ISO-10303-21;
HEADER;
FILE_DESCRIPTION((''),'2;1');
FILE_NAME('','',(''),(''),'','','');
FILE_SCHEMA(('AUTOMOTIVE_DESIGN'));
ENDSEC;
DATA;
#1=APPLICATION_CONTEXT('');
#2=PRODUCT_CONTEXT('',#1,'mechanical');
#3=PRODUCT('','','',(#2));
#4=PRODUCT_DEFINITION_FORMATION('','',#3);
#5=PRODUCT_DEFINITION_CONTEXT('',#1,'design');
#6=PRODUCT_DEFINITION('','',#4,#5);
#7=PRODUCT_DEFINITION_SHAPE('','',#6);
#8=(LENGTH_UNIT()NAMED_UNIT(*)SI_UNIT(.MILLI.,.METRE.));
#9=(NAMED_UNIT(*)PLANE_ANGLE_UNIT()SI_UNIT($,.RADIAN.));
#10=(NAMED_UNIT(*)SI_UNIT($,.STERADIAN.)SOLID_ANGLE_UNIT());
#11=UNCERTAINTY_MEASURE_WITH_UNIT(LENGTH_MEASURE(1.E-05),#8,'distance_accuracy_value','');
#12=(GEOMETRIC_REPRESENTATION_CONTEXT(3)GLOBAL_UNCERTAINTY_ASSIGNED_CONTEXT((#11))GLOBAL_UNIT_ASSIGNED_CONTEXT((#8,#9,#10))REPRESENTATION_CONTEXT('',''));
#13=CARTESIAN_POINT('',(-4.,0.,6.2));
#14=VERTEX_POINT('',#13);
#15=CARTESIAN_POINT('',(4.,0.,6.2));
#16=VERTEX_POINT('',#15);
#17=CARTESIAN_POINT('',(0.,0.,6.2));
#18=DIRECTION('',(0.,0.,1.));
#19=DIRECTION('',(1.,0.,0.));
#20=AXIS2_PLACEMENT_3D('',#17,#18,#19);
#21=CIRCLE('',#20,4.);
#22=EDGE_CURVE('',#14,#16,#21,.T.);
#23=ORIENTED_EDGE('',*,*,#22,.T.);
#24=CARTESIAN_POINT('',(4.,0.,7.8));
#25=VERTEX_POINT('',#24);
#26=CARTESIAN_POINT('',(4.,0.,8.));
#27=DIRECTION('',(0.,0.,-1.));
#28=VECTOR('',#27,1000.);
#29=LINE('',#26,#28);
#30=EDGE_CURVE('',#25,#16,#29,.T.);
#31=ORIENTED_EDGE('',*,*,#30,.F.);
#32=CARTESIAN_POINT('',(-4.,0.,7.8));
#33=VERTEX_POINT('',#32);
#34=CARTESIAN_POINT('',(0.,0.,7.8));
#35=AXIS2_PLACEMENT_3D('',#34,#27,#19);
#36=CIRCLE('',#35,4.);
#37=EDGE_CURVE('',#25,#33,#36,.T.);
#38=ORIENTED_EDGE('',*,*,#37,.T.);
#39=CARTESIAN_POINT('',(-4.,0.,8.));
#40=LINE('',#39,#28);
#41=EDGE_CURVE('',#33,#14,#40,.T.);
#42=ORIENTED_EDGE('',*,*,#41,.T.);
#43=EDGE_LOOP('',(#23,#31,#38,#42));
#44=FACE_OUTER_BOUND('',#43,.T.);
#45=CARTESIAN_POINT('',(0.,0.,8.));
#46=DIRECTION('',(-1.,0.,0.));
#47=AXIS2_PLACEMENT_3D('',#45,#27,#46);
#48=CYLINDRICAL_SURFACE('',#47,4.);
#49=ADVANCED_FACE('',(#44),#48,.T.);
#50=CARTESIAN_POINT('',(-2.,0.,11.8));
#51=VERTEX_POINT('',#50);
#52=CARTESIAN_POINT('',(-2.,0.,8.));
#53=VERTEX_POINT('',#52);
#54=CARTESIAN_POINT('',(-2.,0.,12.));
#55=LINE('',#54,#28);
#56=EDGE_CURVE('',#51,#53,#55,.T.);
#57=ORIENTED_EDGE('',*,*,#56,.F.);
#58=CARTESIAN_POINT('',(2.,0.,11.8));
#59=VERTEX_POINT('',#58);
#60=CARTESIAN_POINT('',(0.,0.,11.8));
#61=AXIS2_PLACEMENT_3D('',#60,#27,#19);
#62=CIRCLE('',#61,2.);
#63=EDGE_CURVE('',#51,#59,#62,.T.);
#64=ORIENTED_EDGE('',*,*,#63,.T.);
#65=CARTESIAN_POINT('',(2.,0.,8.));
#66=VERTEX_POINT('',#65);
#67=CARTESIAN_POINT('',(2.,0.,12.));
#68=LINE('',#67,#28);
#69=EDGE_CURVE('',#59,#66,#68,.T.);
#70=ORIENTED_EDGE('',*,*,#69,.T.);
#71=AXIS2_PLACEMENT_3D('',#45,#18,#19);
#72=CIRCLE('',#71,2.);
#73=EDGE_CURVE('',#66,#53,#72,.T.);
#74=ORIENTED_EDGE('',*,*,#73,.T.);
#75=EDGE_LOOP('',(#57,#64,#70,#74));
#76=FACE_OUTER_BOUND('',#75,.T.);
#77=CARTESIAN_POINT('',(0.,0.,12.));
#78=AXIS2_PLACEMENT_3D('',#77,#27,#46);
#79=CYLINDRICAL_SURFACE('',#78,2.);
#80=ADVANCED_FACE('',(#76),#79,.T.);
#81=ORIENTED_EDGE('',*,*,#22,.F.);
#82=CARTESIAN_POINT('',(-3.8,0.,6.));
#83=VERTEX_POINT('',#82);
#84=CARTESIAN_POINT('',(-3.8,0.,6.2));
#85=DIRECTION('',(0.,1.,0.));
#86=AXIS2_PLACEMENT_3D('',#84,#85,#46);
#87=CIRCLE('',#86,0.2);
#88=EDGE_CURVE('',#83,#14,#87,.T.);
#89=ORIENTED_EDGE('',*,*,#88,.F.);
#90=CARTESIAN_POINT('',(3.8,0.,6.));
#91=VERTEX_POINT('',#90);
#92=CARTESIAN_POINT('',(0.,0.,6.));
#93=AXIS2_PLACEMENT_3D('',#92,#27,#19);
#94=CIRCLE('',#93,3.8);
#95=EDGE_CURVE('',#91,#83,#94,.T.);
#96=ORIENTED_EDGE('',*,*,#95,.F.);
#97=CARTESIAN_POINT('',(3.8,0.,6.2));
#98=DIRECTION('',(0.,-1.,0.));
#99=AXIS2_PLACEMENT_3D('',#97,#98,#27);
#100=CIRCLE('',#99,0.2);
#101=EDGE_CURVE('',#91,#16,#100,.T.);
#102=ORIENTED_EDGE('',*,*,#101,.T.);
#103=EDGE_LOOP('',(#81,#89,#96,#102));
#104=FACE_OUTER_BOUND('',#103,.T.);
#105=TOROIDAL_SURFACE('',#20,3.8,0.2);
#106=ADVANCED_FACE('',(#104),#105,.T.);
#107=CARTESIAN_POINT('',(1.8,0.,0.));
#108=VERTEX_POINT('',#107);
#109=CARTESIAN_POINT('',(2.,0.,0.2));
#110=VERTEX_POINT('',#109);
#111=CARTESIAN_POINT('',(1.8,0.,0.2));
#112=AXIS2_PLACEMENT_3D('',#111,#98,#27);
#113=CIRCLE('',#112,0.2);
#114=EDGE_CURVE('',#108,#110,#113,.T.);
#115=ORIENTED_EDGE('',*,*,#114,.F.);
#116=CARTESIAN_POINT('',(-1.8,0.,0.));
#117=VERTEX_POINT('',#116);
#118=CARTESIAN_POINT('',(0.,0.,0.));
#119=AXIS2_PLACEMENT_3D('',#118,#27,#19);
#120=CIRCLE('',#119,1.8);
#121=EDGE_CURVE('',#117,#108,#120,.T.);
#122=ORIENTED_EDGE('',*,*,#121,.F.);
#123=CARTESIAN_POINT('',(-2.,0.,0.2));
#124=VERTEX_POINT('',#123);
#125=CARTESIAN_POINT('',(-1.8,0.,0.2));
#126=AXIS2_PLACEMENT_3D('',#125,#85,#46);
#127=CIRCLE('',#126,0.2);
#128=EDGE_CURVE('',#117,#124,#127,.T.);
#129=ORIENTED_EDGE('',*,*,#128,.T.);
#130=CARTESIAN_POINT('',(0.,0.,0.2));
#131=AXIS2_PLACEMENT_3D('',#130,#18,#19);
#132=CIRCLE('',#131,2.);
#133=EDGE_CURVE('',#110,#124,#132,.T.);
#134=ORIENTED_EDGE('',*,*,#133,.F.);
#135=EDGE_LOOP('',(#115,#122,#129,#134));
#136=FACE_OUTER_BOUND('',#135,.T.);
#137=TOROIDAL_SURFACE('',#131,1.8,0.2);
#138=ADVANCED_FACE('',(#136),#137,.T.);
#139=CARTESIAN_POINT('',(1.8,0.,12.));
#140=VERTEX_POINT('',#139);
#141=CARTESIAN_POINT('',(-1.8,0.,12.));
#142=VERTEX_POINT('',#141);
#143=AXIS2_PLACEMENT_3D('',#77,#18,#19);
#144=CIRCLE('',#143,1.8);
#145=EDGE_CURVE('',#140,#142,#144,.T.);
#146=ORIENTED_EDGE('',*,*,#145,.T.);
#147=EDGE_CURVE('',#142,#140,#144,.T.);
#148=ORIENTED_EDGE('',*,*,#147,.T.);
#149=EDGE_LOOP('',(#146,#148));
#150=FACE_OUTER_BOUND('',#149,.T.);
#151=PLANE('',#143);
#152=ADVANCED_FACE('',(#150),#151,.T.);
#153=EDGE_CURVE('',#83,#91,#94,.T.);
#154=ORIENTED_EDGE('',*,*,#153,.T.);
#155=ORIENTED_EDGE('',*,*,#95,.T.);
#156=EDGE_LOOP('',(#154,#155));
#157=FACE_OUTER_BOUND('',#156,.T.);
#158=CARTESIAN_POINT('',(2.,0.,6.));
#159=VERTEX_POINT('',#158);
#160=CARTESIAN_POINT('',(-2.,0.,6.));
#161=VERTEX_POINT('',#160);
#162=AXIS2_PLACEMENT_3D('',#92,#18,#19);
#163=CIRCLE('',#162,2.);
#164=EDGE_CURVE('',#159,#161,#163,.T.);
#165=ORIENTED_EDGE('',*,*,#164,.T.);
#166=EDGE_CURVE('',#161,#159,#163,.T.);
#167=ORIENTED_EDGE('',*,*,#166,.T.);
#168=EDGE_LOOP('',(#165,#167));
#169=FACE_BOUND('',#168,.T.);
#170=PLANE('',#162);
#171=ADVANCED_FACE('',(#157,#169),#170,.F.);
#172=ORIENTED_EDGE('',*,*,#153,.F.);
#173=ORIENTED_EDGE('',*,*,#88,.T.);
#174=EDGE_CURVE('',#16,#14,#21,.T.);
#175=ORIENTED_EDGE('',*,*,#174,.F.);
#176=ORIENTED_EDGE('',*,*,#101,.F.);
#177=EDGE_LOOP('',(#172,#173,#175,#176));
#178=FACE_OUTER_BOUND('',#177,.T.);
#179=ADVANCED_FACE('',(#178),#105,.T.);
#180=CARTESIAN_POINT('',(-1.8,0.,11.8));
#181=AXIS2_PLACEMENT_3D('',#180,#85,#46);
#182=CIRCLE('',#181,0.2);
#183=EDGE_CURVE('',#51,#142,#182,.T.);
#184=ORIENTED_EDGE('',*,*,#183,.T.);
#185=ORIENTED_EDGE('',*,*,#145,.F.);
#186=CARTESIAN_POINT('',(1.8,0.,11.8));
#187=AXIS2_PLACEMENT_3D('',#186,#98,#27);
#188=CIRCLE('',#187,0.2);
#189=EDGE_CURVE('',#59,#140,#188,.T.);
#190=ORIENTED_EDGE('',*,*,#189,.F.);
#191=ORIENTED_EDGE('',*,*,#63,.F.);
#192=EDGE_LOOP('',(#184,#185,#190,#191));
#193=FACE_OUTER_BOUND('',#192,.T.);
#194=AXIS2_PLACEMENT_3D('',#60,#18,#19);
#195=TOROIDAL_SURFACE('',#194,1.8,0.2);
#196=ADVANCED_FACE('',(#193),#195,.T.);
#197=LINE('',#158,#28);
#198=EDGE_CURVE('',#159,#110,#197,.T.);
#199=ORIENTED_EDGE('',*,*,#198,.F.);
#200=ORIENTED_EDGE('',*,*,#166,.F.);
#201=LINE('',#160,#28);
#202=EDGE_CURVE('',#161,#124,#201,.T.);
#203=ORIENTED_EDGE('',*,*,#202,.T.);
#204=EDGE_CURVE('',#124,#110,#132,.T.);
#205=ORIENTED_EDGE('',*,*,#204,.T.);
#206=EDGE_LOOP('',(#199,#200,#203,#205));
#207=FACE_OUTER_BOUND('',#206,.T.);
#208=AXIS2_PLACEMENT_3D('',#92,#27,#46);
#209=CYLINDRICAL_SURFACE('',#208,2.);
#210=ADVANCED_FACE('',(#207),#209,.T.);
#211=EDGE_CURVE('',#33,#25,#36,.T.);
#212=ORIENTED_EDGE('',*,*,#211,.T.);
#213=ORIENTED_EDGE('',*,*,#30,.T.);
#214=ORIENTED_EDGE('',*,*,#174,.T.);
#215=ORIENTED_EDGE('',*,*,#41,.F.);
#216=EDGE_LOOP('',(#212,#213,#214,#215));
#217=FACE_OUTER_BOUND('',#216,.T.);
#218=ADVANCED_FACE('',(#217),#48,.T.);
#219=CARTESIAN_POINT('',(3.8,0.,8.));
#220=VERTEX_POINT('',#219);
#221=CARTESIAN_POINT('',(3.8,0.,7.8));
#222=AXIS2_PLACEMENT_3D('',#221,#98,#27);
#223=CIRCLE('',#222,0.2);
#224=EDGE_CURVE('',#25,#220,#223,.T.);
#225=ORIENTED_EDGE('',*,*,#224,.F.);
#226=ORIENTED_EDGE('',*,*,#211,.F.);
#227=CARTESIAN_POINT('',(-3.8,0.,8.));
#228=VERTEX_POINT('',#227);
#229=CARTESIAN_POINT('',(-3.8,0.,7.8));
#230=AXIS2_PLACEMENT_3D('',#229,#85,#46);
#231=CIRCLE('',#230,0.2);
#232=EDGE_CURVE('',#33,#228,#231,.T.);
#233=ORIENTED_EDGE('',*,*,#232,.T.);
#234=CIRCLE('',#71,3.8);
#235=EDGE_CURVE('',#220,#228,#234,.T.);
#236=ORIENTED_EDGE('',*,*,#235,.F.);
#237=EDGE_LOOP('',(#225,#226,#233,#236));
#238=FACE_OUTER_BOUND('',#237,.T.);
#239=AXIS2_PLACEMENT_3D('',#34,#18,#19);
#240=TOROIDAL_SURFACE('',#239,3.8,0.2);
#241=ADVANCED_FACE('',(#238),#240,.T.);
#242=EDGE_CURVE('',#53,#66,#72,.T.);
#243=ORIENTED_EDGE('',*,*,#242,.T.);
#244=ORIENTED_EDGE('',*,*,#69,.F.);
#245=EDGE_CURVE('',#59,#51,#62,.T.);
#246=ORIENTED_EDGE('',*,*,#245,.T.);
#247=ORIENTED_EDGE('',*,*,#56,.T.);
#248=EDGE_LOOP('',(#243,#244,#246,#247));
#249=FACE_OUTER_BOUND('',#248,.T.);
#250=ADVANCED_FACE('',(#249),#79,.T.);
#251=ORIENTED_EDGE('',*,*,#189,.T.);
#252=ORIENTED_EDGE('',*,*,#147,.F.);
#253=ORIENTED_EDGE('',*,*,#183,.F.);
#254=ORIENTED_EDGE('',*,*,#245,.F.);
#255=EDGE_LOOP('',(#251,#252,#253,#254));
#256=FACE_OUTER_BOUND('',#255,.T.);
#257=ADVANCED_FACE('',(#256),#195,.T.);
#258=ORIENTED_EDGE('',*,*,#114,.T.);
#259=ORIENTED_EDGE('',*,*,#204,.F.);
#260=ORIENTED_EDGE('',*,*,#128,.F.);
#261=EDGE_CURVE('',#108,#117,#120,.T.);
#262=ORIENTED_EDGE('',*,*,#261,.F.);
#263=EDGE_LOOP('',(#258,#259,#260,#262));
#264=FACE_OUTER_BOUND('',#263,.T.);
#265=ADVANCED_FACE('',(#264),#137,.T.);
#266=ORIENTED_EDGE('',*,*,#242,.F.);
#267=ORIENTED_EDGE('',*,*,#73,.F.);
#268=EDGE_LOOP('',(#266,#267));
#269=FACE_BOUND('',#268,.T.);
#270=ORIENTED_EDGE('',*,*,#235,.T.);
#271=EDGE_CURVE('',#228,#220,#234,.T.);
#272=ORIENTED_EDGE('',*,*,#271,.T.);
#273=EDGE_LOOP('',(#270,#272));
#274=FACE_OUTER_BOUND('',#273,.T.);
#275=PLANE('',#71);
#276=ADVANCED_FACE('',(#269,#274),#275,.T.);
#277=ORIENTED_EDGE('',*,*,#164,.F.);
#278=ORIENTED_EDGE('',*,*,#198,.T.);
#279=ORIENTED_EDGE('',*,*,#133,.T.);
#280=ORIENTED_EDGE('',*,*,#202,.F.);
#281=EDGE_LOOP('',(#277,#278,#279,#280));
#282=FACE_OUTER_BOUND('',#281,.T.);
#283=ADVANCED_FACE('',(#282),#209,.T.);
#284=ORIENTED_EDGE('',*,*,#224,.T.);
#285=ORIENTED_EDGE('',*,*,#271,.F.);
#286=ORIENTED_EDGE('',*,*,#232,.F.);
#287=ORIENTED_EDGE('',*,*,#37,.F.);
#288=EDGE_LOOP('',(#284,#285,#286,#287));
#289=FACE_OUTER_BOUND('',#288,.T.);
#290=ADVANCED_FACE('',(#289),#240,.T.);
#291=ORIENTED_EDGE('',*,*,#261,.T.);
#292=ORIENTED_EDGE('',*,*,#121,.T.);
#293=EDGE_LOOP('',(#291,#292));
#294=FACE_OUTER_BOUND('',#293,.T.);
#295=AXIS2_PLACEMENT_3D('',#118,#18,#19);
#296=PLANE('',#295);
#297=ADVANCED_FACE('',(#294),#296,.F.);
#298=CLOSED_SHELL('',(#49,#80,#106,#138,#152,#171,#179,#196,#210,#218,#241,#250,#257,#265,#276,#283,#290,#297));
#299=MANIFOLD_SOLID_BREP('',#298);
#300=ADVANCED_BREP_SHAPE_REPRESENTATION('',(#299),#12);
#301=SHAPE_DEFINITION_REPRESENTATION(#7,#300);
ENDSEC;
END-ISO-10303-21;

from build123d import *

# Parameters (mm, degrees)
SKETCH_1_R      = 2
EXTRUDE_1_DEPTH = 6
SKETCH_2_R      = 4
EXTRUDE_2_DEPTH = 2
SKETCH_3_R      = 2
EXTRUDE_3_DEPTH = 4
FILLET_1_R      = 0.2
FILLET_2_R      = 0.2


with BuildPart() as part:
    # 草图1 → 凸台-拉伸1 (new body)
    with BuildSketch(Plane.XY):
        Circle(SKETCH_1_R)
    extrude(amount=EXTRUDE_1_DEPTH)

    # 草图2 → 凸台-拉伸2 (add)
    with BuildSketch(Plane.XY.offset(6)):
        Circle(SKETCH_2_R)
    extrude(amount=EXTRUDE_2_DEPTH)

    # 草图3 → 凸台-拉伸3 (add)
    with BuildSketch(Plane.XY.offset(8)):
        Circle(SKETCH_3_R)
    extrude(amount=EXTRUDE_3_DEPTH)

    # 圆角1
    fillet_1_edges = [part.edges().sort_by_distance(p)[0] for p in [
        (-2, 0, 12),
        (-2, 0, 0),
    ]]
    fillet(fillet_1_edges, radius=FILLET_1_R)

    # 圆角2
    fillet_2_edges = [part.edges().sort_by_distance(p)[0] for p in [
        (-4, 0, 6),
        (-4, 0, 8),
    ]]
    fillet(fillet_2_edges, radius=FILLET_2_R)


solid = part.part
